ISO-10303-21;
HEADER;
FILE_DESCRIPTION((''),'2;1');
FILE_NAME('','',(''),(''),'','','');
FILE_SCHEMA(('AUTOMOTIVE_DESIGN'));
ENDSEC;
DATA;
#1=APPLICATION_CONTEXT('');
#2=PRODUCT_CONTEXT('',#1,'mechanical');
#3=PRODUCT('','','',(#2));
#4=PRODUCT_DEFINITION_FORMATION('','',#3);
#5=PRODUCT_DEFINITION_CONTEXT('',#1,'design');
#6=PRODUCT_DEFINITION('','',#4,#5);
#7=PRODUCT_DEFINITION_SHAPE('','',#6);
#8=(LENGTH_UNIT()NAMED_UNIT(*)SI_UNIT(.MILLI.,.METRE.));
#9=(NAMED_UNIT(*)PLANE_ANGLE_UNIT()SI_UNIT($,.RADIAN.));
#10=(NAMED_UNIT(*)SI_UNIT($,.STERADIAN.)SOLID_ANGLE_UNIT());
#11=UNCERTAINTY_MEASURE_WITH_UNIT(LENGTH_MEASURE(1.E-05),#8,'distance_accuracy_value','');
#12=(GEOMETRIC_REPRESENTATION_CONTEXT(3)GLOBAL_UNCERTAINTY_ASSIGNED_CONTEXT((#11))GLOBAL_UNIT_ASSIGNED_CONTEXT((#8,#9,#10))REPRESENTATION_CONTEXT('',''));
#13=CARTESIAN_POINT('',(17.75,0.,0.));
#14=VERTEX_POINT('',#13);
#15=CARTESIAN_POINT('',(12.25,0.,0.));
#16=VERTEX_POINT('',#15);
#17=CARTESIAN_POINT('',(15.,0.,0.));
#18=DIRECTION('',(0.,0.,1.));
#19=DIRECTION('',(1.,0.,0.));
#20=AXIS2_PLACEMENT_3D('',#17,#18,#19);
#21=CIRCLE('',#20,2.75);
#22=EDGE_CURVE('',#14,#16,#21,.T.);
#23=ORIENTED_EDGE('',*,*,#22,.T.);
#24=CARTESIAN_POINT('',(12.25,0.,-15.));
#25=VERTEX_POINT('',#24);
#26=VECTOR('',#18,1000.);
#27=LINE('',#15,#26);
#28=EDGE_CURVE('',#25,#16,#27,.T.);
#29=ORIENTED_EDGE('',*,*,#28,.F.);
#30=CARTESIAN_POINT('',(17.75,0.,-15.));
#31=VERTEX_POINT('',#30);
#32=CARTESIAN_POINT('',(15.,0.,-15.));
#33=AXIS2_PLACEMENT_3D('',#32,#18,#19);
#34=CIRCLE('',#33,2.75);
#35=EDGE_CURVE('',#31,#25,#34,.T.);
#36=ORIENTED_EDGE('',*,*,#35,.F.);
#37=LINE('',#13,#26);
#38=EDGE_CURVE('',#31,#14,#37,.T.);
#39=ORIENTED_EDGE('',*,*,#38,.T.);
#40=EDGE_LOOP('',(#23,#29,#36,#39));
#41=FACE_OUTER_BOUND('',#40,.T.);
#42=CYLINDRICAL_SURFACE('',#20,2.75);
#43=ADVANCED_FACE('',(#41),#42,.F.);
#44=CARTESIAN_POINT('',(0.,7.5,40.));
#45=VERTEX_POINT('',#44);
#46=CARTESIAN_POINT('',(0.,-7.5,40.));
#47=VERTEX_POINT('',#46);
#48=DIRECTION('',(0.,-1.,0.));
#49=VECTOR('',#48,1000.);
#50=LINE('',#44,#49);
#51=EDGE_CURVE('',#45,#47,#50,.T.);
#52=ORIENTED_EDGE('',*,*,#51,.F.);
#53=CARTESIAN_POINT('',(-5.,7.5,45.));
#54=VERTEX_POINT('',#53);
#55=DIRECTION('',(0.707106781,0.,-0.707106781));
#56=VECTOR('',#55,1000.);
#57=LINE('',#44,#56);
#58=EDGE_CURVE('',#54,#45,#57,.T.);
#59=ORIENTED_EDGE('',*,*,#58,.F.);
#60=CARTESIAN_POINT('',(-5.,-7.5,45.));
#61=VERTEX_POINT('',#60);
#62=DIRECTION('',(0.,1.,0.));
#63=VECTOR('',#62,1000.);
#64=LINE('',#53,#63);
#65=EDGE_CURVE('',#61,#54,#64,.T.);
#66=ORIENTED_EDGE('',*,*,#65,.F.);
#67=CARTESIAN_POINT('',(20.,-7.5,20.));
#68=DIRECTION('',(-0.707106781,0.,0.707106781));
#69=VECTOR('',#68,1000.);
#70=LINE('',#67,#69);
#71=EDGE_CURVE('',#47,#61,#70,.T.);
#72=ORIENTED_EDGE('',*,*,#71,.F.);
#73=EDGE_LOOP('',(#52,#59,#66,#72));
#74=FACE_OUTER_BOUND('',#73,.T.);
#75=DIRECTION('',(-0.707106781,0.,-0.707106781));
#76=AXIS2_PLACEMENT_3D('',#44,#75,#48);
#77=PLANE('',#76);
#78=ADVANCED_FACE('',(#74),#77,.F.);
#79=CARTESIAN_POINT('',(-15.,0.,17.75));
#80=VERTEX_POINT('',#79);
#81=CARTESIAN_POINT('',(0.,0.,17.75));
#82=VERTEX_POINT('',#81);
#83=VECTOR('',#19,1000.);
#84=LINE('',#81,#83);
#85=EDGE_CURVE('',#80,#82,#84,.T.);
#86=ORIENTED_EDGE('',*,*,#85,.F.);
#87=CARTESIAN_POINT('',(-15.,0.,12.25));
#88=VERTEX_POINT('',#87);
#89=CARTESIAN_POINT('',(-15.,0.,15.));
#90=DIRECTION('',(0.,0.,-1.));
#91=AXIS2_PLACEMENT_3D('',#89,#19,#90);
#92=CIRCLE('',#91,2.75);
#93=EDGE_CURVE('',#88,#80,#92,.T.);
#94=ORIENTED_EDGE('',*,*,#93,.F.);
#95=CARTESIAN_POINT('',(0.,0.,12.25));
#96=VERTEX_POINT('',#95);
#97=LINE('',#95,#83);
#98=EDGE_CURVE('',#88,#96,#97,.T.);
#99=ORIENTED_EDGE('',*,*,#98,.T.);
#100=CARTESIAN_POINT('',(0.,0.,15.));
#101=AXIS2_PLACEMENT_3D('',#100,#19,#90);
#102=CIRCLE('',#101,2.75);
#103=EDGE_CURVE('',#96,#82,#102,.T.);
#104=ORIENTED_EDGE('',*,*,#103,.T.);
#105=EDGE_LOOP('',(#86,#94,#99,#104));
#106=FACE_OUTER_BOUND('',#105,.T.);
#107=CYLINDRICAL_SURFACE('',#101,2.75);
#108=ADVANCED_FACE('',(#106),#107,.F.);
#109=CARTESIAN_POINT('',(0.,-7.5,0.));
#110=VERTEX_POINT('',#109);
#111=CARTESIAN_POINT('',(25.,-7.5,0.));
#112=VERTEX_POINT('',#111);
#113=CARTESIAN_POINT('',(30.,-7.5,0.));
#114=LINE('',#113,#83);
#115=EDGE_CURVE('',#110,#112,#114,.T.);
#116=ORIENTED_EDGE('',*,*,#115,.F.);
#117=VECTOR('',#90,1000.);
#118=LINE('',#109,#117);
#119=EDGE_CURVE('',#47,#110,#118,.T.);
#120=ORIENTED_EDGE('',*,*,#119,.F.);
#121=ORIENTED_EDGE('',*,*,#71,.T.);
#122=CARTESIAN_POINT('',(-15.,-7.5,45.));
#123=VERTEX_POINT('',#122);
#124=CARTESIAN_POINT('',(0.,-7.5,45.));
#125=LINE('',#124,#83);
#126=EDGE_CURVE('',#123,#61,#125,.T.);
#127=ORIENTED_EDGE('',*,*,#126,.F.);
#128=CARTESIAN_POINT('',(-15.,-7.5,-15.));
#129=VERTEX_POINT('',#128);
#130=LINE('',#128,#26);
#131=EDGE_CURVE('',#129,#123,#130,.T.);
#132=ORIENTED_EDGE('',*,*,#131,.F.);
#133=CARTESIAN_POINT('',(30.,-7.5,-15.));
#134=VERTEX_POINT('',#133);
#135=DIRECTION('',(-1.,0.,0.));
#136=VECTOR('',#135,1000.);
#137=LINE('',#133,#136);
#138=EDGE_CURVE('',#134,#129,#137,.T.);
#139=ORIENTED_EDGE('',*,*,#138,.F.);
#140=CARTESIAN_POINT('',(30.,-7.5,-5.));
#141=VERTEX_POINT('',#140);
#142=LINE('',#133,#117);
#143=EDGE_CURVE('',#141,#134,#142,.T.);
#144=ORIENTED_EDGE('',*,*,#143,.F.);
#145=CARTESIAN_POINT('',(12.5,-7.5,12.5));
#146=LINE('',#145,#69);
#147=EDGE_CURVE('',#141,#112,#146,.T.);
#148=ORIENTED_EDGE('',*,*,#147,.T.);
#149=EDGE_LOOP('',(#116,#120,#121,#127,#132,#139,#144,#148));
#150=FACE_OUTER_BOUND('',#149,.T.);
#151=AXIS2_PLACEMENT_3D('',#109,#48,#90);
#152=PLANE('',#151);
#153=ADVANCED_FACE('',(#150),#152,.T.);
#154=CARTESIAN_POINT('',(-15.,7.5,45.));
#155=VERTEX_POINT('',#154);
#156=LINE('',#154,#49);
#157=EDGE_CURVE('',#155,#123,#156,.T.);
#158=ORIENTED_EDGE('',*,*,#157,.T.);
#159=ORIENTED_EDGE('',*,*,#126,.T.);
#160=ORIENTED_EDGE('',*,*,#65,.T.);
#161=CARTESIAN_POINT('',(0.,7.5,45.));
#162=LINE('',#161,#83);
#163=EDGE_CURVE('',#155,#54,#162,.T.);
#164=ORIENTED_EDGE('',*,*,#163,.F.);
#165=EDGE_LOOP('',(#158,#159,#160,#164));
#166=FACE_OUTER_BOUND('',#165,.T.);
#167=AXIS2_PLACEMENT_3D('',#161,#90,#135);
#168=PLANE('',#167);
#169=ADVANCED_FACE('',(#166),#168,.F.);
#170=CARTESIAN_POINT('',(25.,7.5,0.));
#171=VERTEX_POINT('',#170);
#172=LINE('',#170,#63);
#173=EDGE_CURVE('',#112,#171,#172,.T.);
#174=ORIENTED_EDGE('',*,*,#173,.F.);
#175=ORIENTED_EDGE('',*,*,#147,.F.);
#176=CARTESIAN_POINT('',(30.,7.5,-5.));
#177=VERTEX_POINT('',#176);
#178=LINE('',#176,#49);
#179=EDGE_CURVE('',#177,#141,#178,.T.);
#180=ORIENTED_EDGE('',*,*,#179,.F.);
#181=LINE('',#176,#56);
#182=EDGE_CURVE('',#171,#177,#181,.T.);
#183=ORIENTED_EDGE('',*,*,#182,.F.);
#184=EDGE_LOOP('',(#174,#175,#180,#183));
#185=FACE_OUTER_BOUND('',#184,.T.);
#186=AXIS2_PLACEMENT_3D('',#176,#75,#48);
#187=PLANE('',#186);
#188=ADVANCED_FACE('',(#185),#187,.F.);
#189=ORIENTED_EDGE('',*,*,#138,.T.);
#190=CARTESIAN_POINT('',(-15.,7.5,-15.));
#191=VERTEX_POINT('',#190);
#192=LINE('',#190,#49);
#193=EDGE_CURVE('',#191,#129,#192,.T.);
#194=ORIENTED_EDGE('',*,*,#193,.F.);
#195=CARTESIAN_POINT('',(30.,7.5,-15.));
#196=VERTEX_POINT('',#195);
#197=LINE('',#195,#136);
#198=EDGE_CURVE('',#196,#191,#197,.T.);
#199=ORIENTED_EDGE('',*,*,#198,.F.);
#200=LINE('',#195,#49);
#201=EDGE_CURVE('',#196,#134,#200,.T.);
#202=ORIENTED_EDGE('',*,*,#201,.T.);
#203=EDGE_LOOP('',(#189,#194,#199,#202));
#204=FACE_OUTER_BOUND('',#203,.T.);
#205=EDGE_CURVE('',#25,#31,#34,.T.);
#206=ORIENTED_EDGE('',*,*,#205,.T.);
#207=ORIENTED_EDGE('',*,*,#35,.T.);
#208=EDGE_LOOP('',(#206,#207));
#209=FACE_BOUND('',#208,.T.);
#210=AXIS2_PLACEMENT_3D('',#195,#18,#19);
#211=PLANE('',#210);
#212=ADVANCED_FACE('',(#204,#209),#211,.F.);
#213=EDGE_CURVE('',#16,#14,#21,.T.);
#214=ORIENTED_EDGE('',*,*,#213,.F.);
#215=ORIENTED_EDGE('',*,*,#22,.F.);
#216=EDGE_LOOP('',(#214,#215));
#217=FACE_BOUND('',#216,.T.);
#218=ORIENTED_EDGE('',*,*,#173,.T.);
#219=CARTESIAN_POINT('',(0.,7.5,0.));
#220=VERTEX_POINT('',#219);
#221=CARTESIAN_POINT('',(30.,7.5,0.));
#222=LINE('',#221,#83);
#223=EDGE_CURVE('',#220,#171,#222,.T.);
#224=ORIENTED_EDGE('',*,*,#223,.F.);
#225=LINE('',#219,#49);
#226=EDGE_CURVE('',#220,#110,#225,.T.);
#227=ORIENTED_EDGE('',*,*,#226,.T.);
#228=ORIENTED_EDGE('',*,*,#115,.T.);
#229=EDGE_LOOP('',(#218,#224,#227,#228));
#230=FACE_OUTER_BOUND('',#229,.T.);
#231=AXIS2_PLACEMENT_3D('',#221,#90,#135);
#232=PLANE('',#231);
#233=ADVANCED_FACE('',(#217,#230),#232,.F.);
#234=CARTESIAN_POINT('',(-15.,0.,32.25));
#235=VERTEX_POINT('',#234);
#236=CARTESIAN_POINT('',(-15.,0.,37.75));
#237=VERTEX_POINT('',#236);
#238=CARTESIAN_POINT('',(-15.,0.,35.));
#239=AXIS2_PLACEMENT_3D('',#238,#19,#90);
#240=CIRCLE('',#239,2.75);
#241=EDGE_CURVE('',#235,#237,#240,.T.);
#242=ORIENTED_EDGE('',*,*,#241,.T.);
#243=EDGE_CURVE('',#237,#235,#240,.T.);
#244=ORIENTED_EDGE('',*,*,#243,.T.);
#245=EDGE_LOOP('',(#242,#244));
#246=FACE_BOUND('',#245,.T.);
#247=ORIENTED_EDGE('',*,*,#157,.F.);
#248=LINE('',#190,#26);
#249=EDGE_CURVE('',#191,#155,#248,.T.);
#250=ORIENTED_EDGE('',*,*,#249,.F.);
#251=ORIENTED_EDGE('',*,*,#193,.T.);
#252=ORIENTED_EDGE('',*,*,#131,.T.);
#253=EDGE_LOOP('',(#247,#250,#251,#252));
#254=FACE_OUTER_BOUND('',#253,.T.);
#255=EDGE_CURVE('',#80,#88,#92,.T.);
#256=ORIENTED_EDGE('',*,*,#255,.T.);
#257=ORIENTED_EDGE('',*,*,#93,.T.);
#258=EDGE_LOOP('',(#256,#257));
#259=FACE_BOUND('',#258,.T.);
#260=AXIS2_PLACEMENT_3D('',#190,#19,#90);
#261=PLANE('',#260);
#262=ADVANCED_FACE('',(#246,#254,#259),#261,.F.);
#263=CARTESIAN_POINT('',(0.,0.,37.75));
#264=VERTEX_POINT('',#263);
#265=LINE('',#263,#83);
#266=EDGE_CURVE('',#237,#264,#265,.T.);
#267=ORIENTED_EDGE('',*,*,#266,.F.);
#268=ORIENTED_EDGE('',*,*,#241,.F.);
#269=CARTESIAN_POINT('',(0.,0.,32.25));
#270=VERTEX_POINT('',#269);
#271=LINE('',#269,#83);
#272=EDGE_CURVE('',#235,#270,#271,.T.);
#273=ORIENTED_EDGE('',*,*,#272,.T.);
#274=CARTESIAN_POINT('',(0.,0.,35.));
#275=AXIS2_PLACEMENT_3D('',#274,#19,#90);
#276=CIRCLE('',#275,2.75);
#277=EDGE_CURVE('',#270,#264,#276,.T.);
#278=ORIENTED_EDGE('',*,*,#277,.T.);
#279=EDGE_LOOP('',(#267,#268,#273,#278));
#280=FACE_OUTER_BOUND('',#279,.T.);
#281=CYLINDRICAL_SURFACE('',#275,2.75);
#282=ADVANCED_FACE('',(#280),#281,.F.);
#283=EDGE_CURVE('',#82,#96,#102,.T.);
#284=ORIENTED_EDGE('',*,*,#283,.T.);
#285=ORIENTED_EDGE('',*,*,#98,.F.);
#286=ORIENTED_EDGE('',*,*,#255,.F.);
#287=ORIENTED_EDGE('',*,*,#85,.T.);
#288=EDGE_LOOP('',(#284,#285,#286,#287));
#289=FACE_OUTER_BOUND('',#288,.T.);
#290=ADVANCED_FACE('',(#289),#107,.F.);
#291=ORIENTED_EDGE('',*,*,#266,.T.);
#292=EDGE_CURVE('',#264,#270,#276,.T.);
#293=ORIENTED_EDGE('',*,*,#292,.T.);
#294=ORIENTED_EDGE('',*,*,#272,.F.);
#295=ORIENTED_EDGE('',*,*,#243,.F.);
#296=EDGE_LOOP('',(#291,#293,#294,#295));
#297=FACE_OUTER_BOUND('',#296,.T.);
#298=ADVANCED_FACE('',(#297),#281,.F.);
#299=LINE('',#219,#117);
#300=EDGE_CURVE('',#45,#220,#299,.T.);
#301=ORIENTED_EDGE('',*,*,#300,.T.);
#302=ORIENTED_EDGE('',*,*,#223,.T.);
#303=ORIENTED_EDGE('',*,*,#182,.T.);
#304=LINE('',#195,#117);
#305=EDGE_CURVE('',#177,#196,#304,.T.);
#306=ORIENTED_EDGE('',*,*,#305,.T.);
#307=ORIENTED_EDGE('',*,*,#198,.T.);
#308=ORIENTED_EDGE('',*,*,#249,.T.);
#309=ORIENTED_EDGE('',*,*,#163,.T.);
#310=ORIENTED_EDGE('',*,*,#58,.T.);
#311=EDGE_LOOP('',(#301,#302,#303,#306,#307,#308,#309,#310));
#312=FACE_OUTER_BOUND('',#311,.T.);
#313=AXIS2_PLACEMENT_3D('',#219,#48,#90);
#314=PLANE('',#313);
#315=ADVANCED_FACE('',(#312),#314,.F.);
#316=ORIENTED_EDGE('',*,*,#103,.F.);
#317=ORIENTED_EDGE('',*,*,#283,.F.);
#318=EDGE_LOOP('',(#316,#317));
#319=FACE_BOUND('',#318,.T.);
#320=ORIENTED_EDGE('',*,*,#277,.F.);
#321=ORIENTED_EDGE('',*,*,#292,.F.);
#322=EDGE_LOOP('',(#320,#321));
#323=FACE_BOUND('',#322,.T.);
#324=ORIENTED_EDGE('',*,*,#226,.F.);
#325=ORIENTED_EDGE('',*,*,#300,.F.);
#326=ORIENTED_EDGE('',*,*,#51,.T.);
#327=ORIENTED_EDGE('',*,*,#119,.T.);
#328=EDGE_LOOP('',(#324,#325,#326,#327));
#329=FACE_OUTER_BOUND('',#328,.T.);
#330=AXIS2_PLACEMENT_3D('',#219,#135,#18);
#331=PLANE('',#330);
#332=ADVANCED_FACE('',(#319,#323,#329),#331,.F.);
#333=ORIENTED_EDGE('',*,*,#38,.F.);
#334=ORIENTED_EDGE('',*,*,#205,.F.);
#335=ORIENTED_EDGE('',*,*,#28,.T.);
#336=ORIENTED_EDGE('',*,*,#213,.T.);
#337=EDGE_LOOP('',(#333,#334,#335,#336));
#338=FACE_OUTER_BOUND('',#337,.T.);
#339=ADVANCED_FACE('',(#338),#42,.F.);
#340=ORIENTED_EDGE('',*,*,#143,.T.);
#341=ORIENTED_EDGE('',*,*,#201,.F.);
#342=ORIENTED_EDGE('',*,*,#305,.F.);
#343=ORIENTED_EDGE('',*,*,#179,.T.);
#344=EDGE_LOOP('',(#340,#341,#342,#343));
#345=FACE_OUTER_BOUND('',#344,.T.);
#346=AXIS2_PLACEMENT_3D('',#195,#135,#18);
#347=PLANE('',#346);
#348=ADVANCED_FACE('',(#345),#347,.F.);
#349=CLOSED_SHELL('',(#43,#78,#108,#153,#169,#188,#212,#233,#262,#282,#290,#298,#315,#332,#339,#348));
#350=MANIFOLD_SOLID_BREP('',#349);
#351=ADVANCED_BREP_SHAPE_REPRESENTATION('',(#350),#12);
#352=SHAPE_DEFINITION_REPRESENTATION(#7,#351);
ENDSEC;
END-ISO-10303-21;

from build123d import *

# Parameters (mm, degrees)
EXTRUDE_1_DEPTH         = 7.5
CHAMFER_1_SIZE          = 5
HOLE_WIZARD_5_5_5_5_1_D = 5.5
HOLE_WIZARD_5_5_5_5_2_D = 5.5


with BuildPart() as part:
    # 草图1 → 凸台-拉伸1 (new, symmetric)
    with BuildSketch(Plane(origin=(0, 0, 0), x_dir=(1, 0, 0), z_dir=(0, 1, 0))):
        Polygon((30, 0), (0, 0), (0, -45), (-15, -45), (-15, 15), (30, 15), align=None)
    extrude(amount=EXTRUDE_1_DEPTH, both=True)

    # 倒角1
    chamfer_1_edges = [part.edges().sort_by_distance(p)[0] for p in [
        (30, 0, 0),
        (0, 0, 45),
    ]]
    chamfer(chamfer_1_edges, length=CHAMFER_1_SIZE)

    # Ø5.5 (5.5) 直径孔1 (through all)
    with Locations(Plane(origin=(0, 0, 0), x_dir=(0, 0, -1), z_dir=(1, 0, 0))):
        with Locations((-35, 0), (-15, 0)):
            Hole(HOLE_WIZARD_5_5_5_5_1_D / 2)

    # Ø5.5 (5.5) 直径孔2 (through all)
    with Locations(Plane.XY):
        with Locations((15, 0)):
            Hole(HOLE_WIZARD_5_5_5_5_2_D / 2)


solid = part.part
